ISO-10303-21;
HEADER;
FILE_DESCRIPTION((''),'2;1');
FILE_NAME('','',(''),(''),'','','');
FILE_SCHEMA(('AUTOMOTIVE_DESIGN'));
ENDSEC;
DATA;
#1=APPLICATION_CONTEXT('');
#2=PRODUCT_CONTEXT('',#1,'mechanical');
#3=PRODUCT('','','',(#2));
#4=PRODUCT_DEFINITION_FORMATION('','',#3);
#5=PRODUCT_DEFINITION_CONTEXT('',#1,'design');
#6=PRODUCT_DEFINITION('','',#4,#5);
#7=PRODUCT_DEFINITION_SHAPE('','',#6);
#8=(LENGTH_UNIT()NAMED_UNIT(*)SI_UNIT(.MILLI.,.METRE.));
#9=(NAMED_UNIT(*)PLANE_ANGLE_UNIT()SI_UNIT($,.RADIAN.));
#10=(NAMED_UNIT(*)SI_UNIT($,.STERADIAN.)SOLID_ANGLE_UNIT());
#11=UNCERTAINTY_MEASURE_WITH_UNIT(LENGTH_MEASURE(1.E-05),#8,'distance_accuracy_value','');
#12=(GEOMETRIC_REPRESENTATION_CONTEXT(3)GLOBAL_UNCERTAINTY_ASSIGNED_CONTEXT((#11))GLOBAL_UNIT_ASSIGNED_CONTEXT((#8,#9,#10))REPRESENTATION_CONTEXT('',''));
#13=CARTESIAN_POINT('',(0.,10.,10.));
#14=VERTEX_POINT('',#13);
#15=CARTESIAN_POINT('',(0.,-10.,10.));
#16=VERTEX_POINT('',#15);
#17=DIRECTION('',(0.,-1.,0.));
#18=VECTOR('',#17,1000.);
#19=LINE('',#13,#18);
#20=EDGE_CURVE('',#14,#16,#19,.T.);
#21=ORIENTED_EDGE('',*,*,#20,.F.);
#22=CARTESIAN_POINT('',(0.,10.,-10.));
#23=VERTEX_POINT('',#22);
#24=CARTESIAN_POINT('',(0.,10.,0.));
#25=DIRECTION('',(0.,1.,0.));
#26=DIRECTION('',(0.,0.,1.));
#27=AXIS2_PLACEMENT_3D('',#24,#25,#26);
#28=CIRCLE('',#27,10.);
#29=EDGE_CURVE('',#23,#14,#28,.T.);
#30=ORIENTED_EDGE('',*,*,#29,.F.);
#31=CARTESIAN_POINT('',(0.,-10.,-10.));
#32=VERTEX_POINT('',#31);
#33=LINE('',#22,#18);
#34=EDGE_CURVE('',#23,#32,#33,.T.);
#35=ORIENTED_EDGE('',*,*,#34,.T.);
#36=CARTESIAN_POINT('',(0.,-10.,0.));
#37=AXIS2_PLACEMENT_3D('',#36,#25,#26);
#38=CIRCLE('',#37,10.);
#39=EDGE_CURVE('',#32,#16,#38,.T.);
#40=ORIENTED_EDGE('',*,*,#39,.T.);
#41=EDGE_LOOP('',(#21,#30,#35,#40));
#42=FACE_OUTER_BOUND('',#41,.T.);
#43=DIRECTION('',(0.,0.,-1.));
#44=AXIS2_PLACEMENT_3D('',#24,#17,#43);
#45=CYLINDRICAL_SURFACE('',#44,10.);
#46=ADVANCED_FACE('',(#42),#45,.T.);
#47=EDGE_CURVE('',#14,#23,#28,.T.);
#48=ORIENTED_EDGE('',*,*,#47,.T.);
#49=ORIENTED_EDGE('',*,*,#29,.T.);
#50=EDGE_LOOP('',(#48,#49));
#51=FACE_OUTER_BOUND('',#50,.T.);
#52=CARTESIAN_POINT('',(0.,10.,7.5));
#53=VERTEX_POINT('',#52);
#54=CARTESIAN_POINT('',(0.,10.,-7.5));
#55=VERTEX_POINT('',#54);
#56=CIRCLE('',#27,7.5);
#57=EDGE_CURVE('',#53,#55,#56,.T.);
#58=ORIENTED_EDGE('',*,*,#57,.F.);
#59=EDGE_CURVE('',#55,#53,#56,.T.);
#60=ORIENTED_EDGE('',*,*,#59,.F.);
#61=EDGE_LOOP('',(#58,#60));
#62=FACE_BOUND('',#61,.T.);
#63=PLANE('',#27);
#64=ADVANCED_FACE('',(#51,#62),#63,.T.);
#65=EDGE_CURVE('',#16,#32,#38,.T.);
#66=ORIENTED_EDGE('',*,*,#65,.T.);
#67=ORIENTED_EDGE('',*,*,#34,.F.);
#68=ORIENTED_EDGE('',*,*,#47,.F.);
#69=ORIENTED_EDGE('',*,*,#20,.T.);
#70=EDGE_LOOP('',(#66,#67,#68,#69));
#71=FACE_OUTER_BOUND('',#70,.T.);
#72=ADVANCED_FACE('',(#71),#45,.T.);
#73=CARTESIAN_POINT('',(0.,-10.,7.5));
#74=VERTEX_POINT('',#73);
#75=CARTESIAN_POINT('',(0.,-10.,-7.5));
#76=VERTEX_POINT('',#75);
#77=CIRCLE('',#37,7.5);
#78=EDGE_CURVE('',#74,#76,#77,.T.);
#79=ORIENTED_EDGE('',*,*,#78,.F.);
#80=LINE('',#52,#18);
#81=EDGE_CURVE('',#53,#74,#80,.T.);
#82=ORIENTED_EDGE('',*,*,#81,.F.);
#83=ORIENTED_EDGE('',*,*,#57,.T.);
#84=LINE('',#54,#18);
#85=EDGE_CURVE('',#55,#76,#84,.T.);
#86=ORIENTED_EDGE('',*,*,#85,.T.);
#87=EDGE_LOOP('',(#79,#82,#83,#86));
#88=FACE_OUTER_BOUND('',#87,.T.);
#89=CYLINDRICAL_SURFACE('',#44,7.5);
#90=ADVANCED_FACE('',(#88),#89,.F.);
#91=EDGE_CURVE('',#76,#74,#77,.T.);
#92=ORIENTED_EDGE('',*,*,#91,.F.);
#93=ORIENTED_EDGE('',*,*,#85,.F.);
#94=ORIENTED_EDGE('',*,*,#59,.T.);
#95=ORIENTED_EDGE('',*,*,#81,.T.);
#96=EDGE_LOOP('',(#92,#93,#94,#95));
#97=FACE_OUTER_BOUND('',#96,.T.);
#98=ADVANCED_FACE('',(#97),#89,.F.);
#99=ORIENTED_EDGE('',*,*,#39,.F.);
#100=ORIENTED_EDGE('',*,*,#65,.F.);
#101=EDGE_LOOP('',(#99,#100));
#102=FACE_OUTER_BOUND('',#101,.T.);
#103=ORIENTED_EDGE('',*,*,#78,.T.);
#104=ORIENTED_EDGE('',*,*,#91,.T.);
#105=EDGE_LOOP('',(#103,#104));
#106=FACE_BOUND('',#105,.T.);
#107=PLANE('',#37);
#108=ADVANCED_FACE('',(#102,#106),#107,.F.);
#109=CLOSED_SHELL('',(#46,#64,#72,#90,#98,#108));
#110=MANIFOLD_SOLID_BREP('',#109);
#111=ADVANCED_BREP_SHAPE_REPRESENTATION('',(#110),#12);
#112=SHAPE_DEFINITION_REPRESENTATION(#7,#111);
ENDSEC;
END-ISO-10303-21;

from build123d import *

# Parameters (mm, degrees)
SKETCH_1_R      = 10
SKETCH_1_R_2    = 7.5
EXTRUDE_1_DEPTH = 10


with BuildPart() as part:
    # 草图1 → 凸台-拉伸1 (new, symmetric)
    with BuildSketch(Plane(origin=(0, 0, 0), x_dir=(1, 0, 0), z_dir=(0, 1, 0))):
        with Locations(Location((0, 0, 0), (0, 0, 270))):
            Circle(SKETCH_1_R)
        with Locations(Location((0, 0, 0), (0, 0, 270))):
            Circle(SKETCH_1_R_2, mode=Mode.SUBTRACT)
    extrude(amount=EXTRUDE_1_DEPTH, both=True)


solid = part.part
